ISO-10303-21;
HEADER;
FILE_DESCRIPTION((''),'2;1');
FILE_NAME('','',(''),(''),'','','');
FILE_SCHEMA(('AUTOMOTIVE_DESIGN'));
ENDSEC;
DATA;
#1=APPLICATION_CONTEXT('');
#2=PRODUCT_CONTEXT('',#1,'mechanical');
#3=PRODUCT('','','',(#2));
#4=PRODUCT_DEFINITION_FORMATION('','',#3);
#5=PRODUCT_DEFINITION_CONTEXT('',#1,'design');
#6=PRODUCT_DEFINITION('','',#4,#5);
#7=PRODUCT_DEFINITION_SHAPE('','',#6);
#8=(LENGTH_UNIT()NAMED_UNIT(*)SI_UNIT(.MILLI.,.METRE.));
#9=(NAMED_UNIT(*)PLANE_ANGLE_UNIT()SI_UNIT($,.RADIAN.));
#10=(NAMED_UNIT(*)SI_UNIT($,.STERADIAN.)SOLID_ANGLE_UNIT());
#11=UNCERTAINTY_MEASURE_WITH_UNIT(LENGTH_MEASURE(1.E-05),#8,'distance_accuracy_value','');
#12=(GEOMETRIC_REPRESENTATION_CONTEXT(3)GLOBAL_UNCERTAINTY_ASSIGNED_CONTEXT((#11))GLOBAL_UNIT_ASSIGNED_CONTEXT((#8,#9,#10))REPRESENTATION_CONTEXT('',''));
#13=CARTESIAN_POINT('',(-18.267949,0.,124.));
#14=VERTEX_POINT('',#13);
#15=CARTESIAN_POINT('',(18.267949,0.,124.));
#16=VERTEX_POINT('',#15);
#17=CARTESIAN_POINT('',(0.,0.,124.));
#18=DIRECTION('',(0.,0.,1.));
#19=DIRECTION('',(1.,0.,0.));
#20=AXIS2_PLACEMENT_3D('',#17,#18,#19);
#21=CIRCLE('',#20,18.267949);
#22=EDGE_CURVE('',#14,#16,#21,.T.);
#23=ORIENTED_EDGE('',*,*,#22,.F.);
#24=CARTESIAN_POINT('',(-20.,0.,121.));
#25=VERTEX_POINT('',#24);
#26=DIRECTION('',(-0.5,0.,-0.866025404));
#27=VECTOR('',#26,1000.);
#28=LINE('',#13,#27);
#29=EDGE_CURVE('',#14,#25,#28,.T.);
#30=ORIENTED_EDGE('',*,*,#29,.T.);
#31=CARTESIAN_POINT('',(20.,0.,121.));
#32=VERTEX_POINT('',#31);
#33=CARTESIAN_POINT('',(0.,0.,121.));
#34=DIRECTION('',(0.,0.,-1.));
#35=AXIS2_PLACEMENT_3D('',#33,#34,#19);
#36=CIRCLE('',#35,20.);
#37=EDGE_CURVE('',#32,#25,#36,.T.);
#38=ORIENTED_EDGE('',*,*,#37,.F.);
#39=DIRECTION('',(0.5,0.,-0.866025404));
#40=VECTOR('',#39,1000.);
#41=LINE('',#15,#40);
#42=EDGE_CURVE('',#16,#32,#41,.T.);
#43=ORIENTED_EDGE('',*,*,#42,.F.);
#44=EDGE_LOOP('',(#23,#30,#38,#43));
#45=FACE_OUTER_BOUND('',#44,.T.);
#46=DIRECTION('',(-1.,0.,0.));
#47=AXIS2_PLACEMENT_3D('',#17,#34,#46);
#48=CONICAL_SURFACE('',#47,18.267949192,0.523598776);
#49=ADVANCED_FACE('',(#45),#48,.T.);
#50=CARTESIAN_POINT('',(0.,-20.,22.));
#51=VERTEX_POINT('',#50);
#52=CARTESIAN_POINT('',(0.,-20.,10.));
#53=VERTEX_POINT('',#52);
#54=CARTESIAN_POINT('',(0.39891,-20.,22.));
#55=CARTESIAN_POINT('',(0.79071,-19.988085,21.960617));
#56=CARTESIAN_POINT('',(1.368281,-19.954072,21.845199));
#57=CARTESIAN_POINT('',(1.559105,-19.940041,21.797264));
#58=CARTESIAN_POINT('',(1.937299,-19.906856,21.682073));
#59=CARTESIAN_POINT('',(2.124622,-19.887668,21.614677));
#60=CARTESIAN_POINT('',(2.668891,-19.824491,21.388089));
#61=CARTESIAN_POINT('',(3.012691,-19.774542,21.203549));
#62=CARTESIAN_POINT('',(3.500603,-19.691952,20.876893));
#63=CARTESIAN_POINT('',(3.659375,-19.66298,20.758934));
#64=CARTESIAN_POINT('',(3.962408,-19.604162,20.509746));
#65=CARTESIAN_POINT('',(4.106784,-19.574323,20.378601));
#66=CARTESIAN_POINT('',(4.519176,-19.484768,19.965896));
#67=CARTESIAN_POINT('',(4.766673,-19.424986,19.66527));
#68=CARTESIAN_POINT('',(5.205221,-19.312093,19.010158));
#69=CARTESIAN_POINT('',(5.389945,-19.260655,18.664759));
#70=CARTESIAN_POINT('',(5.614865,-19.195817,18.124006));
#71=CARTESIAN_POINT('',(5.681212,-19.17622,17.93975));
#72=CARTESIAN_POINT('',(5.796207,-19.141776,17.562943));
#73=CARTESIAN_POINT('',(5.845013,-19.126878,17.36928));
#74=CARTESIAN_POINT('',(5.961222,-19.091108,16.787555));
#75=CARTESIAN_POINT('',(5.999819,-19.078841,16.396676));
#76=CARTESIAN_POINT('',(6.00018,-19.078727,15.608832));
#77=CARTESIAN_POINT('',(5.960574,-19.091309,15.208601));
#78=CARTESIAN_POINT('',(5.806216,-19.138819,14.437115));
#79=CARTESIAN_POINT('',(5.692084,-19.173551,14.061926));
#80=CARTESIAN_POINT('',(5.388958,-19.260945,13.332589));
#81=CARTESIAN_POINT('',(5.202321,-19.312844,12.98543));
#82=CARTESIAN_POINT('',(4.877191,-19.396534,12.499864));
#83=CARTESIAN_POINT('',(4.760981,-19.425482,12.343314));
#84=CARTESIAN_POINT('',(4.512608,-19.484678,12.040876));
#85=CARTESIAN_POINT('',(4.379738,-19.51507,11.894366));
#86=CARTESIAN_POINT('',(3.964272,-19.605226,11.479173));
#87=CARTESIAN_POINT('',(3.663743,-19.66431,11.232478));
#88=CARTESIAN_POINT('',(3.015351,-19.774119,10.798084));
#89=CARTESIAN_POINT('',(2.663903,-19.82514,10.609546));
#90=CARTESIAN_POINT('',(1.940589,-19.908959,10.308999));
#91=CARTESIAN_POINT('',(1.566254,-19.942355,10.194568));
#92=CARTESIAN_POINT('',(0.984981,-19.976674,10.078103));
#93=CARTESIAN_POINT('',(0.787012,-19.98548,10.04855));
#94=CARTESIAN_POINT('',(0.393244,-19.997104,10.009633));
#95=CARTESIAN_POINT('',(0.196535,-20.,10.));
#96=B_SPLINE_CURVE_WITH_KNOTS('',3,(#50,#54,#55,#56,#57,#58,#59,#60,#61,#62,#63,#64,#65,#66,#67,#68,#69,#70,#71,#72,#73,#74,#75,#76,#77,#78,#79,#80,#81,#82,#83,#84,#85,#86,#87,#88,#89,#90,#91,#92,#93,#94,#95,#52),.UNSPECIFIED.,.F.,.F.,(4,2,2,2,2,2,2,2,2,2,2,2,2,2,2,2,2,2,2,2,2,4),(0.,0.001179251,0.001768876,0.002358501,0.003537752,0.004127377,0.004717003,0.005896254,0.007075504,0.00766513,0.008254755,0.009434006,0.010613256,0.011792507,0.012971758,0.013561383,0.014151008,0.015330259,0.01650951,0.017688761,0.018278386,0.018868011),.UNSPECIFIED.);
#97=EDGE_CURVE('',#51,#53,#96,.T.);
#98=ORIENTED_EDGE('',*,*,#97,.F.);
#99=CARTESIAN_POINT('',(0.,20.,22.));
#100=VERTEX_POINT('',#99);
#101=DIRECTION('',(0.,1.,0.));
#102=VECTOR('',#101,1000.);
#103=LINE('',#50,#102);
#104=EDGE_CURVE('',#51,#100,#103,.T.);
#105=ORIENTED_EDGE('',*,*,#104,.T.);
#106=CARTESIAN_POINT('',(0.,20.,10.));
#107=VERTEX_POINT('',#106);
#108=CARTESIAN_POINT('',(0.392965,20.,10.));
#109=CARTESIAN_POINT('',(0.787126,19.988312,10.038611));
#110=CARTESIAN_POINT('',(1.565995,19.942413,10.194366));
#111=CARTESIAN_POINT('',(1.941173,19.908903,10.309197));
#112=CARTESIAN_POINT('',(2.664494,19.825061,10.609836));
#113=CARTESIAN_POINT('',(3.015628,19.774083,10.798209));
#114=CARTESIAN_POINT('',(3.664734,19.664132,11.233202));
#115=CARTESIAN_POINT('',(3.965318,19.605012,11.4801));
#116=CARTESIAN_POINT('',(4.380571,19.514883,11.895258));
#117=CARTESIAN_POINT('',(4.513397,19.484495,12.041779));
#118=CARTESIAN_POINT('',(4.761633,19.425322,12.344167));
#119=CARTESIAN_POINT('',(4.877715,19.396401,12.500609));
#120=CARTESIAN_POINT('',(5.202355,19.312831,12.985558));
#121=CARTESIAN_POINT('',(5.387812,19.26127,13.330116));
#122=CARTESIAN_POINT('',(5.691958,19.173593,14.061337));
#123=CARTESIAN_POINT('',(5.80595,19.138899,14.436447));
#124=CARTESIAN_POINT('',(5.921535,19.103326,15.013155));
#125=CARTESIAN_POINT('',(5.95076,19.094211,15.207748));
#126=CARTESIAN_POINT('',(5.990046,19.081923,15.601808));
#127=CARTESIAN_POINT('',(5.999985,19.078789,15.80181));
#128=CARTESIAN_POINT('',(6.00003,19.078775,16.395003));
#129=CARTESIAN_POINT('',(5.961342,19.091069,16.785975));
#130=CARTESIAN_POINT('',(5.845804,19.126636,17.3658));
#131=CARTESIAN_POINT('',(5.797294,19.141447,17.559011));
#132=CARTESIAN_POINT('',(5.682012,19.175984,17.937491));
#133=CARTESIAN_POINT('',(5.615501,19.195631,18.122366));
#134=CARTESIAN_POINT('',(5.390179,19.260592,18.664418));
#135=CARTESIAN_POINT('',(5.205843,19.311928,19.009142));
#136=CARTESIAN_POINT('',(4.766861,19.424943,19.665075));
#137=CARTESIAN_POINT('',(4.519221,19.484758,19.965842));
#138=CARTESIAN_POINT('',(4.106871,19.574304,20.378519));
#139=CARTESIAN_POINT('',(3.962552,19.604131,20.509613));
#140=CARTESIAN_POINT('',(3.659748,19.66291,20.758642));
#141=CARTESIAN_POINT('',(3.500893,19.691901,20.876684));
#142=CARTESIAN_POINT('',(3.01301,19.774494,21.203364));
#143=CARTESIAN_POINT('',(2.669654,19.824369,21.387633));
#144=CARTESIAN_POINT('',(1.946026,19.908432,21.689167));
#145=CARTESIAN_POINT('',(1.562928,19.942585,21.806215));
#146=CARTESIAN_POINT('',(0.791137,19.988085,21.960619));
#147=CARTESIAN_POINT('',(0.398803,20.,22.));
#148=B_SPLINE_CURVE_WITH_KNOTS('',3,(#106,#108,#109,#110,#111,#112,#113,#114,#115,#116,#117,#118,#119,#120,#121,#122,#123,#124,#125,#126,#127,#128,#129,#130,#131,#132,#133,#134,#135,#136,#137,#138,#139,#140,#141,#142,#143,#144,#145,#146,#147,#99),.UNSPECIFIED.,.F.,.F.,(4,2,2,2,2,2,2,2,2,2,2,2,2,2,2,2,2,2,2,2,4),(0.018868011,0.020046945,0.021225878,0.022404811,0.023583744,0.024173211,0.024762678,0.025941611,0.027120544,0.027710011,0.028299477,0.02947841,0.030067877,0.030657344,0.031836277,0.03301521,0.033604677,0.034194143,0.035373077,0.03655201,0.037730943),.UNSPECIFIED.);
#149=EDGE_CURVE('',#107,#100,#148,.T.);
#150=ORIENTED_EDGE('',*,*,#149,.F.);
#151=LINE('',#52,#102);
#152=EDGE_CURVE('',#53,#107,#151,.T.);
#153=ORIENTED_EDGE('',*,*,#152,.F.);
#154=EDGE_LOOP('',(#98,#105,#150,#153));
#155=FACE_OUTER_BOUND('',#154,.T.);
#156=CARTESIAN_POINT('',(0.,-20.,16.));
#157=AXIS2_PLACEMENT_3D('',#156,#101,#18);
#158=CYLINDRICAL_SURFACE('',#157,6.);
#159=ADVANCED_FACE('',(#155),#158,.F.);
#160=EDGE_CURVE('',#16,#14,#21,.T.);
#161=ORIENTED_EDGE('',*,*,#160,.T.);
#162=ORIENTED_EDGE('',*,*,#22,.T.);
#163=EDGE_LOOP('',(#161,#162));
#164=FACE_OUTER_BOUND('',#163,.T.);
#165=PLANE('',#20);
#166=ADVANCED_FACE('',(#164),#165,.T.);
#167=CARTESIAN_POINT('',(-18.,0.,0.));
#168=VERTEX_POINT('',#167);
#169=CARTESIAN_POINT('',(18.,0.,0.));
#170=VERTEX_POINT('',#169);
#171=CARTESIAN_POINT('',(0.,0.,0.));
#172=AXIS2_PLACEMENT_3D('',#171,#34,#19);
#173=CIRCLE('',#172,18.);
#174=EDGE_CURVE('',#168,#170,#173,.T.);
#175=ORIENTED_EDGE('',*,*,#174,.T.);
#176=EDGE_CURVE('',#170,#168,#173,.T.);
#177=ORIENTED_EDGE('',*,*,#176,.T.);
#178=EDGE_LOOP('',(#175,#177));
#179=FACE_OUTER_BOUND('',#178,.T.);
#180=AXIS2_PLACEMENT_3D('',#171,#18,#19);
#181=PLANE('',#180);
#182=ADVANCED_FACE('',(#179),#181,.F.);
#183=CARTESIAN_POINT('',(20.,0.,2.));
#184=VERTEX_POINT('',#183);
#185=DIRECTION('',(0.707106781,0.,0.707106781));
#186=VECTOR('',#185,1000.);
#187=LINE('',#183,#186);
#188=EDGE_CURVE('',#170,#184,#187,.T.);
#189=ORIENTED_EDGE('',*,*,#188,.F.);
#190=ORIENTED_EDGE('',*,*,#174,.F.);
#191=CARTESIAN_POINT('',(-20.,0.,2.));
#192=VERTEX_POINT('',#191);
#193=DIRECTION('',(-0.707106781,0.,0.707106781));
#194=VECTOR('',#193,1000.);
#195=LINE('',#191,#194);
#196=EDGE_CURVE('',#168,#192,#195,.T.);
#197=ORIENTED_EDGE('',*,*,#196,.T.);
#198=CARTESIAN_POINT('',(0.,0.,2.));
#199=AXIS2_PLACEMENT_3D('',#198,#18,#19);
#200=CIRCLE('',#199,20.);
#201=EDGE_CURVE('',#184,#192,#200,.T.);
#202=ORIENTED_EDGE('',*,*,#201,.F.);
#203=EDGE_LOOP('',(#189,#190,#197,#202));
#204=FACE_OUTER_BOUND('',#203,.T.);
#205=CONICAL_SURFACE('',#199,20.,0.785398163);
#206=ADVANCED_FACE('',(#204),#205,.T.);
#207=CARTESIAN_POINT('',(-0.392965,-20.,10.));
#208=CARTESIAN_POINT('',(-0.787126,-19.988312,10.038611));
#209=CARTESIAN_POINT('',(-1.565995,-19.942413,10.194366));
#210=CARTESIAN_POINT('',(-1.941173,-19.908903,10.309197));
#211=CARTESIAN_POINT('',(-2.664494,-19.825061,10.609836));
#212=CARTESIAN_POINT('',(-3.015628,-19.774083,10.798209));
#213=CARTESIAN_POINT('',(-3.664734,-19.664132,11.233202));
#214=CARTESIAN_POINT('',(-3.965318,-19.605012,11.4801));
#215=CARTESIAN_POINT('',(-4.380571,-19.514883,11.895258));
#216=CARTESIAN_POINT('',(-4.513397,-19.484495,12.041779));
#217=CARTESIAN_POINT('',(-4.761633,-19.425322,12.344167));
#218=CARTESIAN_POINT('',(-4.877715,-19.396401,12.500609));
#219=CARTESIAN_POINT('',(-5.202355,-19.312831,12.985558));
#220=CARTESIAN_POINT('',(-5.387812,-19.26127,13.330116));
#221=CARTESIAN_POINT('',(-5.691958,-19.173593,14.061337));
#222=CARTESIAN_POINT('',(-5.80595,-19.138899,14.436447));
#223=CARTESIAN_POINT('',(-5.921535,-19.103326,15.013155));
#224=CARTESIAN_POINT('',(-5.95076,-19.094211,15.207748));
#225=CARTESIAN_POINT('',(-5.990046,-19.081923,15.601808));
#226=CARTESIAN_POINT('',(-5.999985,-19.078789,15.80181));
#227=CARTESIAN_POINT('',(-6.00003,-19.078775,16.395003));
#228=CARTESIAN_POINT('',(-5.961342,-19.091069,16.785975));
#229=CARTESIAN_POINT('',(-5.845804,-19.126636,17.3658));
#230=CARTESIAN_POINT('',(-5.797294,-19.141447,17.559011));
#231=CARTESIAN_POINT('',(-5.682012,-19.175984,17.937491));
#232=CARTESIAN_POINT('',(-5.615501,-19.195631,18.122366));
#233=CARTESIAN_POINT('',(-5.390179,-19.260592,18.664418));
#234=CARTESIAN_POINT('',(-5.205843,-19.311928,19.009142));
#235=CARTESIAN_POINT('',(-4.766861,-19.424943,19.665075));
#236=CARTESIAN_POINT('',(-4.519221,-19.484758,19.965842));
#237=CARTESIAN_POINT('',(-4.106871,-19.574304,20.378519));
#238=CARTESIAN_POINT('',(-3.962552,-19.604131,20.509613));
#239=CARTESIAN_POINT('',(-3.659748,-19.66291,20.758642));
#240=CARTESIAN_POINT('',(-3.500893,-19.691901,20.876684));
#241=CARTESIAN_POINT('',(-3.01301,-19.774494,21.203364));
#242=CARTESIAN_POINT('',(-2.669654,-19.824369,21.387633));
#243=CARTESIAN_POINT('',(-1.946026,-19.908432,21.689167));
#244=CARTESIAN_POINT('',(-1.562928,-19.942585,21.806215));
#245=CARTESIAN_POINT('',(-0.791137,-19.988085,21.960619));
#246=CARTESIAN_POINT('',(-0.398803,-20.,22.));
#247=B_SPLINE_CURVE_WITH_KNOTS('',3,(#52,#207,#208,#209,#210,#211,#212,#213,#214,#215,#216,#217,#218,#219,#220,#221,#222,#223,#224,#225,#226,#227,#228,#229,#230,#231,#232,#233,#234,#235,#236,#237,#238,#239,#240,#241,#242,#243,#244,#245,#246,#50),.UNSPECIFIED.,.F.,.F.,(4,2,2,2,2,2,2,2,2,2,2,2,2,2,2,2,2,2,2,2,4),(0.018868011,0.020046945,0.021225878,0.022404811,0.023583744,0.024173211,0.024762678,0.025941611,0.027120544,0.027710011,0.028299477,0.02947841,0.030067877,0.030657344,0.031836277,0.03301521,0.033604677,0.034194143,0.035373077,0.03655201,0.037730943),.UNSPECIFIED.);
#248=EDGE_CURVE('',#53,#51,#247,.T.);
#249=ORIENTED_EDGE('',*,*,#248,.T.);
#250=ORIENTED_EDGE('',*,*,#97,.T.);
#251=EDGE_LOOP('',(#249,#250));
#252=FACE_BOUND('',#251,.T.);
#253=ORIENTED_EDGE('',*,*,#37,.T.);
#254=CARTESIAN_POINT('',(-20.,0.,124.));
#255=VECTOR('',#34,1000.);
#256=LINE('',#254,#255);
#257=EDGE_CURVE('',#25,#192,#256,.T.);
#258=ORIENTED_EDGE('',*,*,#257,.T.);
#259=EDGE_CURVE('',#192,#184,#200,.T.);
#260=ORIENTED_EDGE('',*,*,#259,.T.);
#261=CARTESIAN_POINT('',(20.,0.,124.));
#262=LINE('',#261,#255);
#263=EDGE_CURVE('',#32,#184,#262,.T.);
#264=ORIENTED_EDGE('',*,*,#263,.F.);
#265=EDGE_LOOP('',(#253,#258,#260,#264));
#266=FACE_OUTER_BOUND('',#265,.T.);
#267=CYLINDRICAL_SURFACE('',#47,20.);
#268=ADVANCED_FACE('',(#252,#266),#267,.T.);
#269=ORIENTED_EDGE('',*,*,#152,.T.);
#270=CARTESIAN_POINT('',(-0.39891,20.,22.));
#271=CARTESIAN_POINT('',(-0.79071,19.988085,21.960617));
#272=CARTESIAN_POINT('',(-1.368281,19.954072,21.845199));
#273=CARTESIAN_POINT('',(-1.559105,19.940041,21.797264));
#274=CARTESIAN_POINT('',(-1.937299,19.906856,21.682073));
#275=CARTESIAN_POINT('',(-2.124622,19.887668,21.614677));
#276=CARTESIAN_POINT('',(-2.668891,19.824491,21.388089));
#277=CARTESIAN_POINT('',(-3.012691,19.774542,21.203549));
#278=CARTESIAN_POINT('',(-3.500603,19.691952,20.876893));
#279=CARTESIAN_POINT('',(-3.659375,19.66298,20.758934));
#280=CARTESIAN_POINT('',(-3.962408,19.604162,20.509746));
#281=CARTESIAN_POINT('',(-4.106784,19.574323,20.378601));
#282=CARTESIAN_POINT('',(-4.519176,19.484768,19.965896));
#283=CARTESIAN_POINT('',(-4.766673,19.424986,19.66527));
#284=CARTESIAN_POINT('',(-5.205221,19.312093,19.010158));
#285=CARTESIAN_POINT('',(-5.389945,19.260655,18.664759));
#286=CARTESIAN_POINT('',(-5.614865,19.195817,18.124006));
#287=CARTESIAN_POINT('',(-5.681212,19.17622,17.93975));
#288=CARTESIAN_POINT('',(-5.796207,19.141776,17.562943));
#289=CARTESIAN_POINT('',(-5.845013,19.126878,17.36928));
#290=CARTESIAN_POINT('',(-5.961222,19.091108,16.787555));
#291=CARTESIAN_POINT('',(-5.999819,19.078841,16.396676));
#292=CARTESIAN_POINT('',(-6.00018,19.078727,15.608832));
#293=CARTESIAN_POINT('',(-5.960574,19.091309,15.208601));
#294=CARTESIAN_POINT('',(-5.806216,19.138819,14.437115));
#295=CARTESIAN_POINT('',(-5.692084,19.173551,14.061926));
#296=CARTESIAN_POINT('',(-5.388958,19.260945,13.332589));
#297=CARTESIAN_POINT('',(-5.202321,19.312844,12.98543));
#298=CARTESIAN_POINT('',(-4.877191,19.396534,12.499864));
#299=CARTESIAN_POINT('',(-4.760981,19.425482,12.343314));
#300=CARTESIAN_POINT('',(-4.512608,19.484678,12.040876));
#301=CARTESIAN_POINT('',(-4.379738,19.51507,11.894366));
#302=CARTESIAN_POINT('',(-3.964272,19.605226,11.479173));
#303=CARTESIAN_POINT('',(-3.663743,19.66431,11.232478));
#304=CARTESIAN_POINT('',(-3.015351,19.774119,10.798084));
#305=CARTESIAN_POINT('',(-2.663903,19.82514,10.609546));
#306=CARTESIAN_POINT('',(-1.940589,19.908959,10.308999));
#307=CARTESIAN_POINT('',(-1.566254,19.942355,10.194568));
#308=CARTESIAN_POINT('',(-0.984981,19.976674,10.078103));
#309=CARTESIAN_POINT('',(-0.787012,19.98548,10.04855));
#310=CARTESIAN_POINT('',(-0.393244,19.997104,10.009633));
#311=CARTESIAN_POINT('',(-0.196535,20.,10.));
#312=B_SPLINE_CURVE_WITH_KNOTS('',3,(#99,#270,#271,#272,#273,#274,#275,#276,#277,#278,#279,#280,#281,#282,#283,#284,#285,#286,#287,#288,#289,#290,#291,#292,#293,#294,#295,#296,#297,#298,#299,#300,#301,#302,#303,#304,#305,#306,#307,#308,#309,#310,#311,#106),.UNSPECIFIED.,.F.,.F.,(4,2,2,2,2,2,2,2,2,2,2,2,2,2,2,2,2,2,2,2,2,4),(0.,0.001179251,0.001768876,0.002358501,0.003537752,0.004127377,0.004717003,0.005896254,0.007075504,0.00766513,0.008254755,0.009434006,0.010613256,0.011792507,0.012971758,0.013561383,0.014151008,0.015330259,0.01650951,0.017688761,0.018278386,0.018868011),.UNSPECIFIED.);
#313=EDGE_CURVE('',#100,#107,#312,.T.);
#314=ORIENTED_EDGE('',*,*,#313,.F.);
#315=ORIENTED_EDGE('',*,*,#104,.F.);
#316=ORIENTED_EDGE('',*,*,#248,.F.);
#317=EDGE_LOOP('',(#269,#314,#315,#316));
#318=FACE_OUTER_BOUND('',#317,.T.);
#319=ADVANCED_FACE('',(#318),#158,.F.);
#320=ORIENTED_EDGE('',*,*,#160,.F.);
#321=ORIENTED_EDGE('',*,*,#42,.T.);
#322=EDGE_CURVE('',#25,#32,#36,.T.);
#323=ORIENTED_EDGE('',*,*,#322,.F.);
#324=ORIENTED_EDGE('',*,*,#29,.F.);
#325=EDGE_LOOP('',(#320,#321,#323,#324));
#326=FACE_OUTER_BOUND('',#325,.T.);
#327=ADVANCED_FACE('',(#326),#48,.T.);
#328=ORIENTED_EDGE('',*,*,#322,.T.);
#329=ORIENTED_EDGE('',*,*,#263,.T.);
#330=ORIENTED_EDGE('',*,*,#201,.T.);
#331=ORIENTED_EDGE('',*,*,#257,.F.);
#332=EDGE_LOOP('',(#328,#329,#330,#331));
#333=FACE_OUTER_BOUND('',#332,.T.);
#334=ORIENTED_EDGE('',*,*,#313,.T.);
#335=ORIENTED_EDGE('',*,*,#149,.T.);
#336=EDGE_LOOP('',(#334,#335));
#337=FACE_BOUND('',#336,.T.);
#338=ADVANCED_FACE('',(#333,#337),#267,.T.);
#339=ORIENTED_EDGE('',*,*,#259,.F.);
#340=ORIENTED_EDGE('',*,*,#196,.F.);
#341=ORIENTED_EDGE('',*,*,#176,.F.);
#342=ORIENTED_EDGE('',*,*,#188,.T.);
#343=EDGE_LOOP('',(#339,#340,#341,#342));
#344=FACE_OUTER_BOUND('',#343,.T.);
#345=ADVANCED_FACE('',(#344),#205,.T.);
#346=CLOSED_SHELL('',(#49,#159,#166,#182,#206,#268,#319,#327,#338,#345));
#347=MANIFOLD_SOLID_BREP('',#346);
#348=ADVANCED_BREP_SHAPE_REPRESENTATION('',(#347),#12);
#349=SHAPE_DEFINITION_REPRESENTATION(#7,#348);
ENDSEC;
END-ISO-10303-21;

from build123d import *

# Parameters (mm, degrees)
SKETCH_1_R               = 20
EXTRUDE_1_DEPTH          = 124
CHAMFER_1_SIZE           = 3
CHAMFER_1_SIZE2          = 1.732050808
CHAMFER_3_SIZE           = 2
CUT_EXTRUDE_2_DEPTH      = 128.184904765
CUT_EXTRUDE_2_DEPTH_BACK = 128.184904765
SKETCH_3_R               = 6


with BuildPart() as part:
    # 草图1 → 凸台-拉伸1 (new body)
    with BuildSketch(Plane.XY):
        Circle(SKETCH_1_R)
    extrude(amount=EXTRUDE_1_DEPTH)

    # 倒角1
    chamfer_1_edges = [part.edges().sort_by_distance(p)[0] for p in [
        (-20, 0, 124),
    ]]
    chamfer_1_side = [part.faces().sort_by_distance(p)[0] for p in [
        (-20, 0, 62),
    ]]
    chamfer(chamfer_1_edges, length=CHAMFER_1_SIZE, length2=CHAMFER_1_SIZE2, reference=chamfer_1_side[0])

    # 倒角3
    chamfer_3_edges = [part.edges().sort_by_distance(p)[0] for p in [
        (-20, 0, 0),
    ]]
    chamfer(chamfer_3_edges, length=CHAMFER_3_SIZE)

    # 草图3 → 切除-拉伸2 (cut, two sides: drawn at the far end of the back side and taken through both)
    with BuildSketch(Plane(origin=(0, 0, 0), x_dir=(1, 0, 0), z_dir=(0, 1, 0)).offset(-CUT_EXTRUDE_2_DEPTH_BACK)):
        with Locations(Location((0, -16, 0), (0, 0, 270))):
            Circle(SKETCH_3_R)
    extrude(amount=CUT_EXTRUDE_2_DEPTH + CUT_EXTRUDE_2_DEPTH_BACK, mode=Mode.SUBTRACT)


solid = part.part
